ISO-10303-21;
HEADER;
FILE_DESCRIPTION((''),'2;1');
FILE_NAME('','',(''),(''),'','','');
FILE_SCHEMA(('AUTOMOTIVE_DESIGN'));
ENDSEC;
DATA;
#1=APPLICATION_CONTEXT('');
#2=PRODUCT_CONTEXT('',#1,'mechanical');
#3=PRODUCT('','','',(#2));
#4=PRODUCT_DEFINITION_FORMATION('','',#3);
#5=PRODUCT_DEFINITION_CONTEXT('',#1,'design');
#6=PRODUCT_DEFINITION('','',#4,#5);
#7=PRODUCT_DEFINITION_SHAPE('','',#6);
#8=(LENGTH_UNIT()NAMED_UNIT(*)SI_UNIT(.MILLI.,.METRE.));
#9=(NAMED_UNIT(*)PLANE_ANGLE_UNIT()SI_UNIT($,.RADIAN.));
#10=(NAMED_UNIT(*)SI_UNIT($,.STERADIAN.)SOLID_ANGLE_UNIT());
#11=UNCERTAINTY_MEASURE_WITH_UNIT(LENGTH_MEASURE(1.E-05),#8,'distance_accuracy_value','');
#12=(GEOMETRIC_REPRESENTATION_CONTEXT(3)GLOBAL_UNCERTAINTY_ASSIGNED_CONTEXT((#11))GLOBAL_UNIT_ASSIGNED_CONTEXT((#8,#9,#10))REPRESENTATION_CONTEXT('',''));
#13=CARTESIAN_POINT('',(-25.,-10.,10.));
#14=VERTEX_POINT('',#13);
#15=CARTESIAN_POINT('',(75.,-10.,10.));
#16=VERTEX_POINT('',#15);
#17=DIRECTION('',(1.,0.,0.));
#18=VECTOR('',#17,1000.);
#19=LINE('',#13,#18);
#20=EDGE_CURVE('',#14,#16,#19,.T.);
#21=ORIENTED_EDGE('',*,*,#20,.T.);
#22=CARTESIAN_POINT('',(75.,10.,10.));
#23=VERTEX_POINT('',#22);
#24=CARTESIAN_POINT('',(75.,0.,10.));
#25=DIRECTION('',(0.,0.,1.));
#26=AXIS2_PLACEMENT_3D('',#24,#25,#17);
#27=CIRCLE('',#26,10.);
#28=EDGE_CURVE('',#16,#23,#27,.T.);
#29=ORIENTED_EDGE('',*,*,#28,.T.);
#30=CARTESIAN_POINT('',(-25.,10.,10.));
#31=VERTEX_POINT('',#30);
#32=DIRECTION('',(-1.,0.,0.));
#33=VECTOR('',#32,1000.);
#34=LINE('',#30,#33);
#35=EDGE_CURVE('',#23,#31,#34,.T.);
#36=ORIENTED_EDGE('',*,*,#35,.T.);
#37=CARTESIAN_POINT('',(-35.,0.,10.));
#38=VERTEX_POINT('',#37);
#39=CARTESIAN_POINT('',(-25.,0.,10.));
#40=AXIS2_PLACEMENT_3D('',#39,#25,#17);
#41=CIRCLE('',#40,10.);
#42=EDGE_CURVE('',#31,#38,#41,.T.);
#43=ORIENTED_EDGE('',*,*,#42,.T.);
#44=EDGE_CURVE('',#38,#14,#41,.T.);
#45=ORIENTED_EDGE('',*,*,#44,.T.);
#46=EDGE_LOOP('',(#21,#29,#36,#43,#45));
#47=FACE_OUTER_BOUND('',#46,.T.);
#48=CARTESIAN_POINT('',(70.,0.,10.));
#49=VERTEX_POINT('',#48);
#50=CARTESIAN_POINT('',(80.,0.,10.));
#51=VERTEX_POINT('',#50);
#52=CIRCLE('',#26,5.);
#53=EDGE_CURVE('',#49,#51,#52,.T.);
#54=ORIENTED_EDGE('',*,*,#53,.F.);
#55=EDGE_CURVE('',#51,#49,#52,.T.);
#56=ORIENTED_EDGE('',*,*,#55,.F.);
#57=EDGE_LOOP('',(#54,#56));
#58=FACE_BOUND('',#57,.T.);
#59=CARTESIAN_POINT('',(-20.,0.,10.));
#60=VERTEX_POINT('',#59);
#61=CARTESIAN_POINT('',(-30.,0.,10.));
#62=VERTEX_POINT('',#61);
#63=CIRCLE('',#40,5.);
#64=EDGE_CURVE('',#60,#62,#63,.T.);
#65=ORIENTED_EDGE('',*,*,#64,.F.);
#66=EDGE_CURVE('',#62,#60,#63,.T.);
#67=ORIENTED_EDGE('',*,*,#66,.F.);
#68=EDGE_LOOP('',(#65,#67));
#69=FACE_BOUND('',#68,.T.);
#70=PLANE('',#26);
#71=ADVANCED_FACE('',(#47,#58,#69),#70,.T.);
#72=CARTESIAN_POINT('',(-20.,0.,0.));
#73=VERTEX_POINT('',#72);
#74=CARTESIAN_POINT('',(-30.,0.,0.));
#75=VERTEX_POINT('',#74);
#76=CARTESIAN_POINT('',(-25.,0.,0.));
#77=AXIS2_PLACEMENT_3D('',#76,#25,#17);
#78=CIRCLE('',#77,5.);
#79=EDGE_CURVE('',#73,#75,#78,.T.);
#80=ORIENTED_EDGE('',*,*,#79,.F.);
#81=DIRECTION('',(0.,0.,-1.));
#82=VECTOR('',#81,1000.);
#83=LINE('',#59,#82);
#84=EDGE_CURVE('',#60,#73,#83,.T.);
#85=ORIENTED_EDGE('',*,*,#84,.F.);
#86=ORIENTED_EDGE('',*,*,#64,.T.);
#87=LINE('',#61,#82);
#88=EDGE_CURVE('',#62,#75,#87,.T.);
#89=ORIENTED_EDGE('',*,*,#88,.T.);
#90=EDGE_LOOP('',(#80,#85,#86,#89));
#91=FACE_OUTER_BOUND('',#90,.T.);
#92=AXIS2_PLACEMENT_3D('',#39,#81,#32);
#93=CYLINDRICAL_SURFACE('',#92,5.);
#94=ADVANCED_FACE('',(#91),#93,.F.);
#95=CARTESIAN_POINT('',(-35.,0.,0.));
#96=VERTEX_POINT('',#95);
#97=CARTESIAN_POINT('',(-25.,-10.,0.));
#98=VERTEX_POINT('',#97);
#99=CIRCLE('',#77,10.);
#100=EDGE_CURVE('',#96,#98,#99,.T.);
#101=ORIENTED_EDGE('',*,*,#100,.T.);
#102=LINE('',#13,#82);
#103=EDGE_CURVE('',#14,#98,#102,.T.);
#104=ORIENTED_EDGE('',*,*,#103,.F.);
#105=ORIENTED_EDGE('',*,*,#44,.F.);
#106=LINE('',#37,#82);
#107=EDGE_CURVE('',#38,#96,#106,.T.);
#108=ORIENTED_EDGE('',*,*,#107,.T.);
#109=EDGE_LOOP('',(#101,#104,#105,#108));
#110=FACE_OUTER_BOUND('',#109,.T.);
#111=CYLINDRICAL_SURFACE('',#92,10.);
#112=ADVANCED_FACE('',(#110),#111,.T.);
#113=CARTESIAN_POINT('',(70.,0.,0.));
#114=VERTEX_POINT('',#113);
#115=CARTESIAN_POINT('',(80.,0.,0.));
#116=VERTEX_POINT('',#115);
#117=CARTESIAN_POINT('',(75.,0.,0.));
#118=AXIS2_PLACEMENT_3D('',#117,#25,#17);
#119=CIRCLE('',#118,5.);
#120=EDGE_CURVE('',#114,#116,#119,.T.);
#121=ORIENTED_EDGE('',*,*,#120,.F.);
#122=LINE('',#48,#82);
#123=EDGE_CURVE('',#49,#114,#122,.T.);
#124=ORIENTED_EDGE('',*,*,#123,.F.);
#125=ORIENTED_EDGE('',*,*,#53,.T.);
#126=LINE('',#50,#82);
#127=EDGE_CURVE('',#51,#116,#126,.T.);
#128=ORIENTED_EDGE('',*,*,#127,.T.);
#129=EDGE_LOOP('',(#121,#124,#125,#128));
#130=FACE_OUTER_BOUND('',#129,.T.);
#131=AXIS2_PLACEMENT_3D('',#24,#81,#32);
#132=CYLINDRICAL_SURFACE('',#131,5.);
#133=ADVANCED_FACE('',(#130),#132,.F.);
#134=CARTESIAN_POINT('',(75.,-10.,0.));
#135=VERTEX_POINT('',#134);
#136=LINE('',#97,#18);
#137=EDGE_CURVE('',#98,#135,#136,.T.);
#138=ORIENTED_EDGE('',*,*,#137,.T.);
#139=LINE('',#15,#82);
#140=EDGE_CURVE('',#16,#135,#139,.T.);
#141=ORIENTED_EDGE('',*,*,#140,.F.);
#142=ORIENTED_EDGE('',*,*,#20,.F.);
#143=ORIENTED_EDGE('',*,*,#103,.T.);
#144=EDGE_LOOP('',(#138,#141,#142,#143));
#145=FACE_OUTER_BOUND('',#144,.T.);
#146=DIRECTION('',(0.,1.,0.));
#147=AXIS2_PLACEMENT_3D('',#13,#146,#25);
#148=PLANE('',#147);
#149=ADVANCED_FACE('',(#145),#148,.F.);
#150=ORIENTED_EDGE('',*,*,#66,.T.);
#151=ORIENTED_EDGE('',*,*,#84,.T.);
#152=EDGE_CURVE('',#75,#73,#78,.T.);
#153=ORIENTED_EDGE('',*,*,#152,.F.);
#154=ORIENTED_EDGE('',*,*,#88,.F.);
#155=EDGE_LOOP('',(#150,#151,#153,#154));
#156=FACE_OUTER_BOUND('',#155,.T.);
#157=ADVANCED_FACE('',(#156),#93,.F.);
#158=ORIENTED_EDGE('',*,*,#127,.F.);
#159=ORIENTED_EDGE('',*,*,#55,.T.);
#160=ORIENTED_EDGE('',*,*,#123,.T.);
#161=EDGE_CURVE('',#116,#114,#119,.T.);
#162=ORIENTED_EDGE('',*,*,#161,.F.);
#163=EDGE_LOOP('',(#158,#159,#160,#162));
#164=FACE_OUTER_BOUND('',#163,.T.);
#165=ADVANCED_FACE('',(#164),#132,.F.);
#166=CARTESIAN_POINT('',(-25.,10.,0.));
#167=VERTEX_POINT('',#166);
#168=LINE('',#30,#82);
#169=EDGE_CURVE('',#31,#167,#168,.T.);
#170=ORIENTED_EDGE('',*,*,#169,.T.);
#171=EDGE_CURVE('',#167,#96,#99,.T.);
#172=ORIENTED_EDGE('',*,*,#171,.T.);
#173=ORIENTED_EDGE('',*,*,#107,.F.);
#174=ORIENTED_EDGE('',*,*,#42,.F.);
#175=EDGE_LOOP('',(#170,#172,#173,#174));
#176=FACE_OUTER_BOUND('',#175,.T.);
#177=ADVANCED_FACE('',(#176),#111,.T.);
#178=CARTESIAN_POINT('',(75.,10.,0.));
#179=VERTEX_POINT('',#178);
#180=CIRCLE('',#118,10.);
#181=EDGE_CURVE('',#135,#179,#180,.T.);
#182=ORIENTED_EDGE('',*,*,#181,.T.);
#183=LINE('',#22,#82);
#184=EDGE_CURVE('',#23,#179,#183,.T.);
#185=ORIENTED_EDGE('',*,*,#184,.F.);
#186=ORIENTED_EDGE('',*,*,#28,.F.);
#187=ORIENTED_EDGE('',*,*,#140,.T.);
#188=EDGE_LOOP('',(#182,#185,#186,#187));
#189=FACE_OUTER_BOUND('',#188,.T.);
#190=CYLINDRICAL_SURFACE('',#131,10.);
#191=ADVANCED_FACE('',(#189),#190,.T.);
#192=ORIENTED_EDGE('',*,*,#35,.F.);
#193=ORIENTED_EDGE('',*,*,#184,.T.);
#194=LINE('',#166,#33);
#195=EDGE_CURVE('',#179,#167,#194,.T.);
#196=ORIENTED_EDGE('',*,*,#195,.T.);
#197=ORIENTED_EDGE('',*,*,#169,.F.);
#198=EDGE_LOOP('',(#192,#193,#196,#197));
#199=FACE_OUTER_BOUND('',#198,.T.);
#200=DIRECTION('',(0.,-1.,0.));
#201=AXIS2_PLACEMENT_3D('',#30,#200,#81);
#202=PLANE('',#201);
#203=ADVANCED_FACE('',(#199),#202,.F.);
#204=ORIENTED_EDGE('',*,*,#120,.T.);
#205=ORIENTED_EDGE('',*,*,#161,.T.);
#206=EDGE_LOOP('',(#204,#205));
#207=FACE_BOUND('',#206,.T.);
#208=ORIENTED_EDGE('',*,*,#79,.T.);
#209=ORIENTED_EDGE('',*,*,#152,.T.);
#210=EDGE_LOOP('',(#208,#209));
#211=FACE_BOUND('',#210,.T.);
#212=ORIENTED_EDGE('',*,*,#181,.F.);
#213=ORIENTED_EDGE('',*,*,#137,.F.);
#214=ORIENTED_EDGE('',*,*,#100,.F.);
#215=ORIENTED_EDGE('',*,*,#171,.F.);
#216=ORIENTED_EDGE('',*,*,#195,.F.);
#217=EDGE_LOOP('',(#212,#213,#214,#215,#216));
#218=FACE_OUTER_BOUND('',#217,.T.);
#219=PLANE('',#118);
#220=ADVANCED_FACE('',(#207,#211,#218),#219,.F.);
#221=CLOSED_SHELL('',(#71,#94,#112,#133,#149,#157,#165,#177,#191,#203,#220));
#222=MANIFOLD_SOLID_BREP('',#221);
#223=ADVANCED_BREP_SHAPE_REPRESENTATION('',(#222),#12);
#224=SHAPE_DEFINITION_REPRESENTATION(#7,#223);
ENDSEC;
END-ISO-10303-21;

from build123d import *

# Parameters (mm, degrees)
SKETCH1_R           = 5
BOSS_EXTRUDE1_DEPTH = 10


with BuildPart() as part:
    # Sketch1 → Boss-Extrude1 (new body)
    with BuildSketch(Plane.XY):
        with BuildLine():
            Line((-25, 10), (75, 10))
            ThreePointArc((75, 10), (85, 0), (75, -10))
            Line((75, -10), (-25, -10))
            ThreePointArc((-25, -10), (-35, 0), (-25, 10))
        make_face()
        with Locations((75, 0)):
            Circle(SKETCH1_R, mode=Mode.SUBTRACT)
        with Locations((-25, 0)):
            Circle(SKETCH1_R, mode=Mode.SUBTRACT)
    extrude(amount=BOSS_EXTRUDE1_DEPTH)


solid = part.part
